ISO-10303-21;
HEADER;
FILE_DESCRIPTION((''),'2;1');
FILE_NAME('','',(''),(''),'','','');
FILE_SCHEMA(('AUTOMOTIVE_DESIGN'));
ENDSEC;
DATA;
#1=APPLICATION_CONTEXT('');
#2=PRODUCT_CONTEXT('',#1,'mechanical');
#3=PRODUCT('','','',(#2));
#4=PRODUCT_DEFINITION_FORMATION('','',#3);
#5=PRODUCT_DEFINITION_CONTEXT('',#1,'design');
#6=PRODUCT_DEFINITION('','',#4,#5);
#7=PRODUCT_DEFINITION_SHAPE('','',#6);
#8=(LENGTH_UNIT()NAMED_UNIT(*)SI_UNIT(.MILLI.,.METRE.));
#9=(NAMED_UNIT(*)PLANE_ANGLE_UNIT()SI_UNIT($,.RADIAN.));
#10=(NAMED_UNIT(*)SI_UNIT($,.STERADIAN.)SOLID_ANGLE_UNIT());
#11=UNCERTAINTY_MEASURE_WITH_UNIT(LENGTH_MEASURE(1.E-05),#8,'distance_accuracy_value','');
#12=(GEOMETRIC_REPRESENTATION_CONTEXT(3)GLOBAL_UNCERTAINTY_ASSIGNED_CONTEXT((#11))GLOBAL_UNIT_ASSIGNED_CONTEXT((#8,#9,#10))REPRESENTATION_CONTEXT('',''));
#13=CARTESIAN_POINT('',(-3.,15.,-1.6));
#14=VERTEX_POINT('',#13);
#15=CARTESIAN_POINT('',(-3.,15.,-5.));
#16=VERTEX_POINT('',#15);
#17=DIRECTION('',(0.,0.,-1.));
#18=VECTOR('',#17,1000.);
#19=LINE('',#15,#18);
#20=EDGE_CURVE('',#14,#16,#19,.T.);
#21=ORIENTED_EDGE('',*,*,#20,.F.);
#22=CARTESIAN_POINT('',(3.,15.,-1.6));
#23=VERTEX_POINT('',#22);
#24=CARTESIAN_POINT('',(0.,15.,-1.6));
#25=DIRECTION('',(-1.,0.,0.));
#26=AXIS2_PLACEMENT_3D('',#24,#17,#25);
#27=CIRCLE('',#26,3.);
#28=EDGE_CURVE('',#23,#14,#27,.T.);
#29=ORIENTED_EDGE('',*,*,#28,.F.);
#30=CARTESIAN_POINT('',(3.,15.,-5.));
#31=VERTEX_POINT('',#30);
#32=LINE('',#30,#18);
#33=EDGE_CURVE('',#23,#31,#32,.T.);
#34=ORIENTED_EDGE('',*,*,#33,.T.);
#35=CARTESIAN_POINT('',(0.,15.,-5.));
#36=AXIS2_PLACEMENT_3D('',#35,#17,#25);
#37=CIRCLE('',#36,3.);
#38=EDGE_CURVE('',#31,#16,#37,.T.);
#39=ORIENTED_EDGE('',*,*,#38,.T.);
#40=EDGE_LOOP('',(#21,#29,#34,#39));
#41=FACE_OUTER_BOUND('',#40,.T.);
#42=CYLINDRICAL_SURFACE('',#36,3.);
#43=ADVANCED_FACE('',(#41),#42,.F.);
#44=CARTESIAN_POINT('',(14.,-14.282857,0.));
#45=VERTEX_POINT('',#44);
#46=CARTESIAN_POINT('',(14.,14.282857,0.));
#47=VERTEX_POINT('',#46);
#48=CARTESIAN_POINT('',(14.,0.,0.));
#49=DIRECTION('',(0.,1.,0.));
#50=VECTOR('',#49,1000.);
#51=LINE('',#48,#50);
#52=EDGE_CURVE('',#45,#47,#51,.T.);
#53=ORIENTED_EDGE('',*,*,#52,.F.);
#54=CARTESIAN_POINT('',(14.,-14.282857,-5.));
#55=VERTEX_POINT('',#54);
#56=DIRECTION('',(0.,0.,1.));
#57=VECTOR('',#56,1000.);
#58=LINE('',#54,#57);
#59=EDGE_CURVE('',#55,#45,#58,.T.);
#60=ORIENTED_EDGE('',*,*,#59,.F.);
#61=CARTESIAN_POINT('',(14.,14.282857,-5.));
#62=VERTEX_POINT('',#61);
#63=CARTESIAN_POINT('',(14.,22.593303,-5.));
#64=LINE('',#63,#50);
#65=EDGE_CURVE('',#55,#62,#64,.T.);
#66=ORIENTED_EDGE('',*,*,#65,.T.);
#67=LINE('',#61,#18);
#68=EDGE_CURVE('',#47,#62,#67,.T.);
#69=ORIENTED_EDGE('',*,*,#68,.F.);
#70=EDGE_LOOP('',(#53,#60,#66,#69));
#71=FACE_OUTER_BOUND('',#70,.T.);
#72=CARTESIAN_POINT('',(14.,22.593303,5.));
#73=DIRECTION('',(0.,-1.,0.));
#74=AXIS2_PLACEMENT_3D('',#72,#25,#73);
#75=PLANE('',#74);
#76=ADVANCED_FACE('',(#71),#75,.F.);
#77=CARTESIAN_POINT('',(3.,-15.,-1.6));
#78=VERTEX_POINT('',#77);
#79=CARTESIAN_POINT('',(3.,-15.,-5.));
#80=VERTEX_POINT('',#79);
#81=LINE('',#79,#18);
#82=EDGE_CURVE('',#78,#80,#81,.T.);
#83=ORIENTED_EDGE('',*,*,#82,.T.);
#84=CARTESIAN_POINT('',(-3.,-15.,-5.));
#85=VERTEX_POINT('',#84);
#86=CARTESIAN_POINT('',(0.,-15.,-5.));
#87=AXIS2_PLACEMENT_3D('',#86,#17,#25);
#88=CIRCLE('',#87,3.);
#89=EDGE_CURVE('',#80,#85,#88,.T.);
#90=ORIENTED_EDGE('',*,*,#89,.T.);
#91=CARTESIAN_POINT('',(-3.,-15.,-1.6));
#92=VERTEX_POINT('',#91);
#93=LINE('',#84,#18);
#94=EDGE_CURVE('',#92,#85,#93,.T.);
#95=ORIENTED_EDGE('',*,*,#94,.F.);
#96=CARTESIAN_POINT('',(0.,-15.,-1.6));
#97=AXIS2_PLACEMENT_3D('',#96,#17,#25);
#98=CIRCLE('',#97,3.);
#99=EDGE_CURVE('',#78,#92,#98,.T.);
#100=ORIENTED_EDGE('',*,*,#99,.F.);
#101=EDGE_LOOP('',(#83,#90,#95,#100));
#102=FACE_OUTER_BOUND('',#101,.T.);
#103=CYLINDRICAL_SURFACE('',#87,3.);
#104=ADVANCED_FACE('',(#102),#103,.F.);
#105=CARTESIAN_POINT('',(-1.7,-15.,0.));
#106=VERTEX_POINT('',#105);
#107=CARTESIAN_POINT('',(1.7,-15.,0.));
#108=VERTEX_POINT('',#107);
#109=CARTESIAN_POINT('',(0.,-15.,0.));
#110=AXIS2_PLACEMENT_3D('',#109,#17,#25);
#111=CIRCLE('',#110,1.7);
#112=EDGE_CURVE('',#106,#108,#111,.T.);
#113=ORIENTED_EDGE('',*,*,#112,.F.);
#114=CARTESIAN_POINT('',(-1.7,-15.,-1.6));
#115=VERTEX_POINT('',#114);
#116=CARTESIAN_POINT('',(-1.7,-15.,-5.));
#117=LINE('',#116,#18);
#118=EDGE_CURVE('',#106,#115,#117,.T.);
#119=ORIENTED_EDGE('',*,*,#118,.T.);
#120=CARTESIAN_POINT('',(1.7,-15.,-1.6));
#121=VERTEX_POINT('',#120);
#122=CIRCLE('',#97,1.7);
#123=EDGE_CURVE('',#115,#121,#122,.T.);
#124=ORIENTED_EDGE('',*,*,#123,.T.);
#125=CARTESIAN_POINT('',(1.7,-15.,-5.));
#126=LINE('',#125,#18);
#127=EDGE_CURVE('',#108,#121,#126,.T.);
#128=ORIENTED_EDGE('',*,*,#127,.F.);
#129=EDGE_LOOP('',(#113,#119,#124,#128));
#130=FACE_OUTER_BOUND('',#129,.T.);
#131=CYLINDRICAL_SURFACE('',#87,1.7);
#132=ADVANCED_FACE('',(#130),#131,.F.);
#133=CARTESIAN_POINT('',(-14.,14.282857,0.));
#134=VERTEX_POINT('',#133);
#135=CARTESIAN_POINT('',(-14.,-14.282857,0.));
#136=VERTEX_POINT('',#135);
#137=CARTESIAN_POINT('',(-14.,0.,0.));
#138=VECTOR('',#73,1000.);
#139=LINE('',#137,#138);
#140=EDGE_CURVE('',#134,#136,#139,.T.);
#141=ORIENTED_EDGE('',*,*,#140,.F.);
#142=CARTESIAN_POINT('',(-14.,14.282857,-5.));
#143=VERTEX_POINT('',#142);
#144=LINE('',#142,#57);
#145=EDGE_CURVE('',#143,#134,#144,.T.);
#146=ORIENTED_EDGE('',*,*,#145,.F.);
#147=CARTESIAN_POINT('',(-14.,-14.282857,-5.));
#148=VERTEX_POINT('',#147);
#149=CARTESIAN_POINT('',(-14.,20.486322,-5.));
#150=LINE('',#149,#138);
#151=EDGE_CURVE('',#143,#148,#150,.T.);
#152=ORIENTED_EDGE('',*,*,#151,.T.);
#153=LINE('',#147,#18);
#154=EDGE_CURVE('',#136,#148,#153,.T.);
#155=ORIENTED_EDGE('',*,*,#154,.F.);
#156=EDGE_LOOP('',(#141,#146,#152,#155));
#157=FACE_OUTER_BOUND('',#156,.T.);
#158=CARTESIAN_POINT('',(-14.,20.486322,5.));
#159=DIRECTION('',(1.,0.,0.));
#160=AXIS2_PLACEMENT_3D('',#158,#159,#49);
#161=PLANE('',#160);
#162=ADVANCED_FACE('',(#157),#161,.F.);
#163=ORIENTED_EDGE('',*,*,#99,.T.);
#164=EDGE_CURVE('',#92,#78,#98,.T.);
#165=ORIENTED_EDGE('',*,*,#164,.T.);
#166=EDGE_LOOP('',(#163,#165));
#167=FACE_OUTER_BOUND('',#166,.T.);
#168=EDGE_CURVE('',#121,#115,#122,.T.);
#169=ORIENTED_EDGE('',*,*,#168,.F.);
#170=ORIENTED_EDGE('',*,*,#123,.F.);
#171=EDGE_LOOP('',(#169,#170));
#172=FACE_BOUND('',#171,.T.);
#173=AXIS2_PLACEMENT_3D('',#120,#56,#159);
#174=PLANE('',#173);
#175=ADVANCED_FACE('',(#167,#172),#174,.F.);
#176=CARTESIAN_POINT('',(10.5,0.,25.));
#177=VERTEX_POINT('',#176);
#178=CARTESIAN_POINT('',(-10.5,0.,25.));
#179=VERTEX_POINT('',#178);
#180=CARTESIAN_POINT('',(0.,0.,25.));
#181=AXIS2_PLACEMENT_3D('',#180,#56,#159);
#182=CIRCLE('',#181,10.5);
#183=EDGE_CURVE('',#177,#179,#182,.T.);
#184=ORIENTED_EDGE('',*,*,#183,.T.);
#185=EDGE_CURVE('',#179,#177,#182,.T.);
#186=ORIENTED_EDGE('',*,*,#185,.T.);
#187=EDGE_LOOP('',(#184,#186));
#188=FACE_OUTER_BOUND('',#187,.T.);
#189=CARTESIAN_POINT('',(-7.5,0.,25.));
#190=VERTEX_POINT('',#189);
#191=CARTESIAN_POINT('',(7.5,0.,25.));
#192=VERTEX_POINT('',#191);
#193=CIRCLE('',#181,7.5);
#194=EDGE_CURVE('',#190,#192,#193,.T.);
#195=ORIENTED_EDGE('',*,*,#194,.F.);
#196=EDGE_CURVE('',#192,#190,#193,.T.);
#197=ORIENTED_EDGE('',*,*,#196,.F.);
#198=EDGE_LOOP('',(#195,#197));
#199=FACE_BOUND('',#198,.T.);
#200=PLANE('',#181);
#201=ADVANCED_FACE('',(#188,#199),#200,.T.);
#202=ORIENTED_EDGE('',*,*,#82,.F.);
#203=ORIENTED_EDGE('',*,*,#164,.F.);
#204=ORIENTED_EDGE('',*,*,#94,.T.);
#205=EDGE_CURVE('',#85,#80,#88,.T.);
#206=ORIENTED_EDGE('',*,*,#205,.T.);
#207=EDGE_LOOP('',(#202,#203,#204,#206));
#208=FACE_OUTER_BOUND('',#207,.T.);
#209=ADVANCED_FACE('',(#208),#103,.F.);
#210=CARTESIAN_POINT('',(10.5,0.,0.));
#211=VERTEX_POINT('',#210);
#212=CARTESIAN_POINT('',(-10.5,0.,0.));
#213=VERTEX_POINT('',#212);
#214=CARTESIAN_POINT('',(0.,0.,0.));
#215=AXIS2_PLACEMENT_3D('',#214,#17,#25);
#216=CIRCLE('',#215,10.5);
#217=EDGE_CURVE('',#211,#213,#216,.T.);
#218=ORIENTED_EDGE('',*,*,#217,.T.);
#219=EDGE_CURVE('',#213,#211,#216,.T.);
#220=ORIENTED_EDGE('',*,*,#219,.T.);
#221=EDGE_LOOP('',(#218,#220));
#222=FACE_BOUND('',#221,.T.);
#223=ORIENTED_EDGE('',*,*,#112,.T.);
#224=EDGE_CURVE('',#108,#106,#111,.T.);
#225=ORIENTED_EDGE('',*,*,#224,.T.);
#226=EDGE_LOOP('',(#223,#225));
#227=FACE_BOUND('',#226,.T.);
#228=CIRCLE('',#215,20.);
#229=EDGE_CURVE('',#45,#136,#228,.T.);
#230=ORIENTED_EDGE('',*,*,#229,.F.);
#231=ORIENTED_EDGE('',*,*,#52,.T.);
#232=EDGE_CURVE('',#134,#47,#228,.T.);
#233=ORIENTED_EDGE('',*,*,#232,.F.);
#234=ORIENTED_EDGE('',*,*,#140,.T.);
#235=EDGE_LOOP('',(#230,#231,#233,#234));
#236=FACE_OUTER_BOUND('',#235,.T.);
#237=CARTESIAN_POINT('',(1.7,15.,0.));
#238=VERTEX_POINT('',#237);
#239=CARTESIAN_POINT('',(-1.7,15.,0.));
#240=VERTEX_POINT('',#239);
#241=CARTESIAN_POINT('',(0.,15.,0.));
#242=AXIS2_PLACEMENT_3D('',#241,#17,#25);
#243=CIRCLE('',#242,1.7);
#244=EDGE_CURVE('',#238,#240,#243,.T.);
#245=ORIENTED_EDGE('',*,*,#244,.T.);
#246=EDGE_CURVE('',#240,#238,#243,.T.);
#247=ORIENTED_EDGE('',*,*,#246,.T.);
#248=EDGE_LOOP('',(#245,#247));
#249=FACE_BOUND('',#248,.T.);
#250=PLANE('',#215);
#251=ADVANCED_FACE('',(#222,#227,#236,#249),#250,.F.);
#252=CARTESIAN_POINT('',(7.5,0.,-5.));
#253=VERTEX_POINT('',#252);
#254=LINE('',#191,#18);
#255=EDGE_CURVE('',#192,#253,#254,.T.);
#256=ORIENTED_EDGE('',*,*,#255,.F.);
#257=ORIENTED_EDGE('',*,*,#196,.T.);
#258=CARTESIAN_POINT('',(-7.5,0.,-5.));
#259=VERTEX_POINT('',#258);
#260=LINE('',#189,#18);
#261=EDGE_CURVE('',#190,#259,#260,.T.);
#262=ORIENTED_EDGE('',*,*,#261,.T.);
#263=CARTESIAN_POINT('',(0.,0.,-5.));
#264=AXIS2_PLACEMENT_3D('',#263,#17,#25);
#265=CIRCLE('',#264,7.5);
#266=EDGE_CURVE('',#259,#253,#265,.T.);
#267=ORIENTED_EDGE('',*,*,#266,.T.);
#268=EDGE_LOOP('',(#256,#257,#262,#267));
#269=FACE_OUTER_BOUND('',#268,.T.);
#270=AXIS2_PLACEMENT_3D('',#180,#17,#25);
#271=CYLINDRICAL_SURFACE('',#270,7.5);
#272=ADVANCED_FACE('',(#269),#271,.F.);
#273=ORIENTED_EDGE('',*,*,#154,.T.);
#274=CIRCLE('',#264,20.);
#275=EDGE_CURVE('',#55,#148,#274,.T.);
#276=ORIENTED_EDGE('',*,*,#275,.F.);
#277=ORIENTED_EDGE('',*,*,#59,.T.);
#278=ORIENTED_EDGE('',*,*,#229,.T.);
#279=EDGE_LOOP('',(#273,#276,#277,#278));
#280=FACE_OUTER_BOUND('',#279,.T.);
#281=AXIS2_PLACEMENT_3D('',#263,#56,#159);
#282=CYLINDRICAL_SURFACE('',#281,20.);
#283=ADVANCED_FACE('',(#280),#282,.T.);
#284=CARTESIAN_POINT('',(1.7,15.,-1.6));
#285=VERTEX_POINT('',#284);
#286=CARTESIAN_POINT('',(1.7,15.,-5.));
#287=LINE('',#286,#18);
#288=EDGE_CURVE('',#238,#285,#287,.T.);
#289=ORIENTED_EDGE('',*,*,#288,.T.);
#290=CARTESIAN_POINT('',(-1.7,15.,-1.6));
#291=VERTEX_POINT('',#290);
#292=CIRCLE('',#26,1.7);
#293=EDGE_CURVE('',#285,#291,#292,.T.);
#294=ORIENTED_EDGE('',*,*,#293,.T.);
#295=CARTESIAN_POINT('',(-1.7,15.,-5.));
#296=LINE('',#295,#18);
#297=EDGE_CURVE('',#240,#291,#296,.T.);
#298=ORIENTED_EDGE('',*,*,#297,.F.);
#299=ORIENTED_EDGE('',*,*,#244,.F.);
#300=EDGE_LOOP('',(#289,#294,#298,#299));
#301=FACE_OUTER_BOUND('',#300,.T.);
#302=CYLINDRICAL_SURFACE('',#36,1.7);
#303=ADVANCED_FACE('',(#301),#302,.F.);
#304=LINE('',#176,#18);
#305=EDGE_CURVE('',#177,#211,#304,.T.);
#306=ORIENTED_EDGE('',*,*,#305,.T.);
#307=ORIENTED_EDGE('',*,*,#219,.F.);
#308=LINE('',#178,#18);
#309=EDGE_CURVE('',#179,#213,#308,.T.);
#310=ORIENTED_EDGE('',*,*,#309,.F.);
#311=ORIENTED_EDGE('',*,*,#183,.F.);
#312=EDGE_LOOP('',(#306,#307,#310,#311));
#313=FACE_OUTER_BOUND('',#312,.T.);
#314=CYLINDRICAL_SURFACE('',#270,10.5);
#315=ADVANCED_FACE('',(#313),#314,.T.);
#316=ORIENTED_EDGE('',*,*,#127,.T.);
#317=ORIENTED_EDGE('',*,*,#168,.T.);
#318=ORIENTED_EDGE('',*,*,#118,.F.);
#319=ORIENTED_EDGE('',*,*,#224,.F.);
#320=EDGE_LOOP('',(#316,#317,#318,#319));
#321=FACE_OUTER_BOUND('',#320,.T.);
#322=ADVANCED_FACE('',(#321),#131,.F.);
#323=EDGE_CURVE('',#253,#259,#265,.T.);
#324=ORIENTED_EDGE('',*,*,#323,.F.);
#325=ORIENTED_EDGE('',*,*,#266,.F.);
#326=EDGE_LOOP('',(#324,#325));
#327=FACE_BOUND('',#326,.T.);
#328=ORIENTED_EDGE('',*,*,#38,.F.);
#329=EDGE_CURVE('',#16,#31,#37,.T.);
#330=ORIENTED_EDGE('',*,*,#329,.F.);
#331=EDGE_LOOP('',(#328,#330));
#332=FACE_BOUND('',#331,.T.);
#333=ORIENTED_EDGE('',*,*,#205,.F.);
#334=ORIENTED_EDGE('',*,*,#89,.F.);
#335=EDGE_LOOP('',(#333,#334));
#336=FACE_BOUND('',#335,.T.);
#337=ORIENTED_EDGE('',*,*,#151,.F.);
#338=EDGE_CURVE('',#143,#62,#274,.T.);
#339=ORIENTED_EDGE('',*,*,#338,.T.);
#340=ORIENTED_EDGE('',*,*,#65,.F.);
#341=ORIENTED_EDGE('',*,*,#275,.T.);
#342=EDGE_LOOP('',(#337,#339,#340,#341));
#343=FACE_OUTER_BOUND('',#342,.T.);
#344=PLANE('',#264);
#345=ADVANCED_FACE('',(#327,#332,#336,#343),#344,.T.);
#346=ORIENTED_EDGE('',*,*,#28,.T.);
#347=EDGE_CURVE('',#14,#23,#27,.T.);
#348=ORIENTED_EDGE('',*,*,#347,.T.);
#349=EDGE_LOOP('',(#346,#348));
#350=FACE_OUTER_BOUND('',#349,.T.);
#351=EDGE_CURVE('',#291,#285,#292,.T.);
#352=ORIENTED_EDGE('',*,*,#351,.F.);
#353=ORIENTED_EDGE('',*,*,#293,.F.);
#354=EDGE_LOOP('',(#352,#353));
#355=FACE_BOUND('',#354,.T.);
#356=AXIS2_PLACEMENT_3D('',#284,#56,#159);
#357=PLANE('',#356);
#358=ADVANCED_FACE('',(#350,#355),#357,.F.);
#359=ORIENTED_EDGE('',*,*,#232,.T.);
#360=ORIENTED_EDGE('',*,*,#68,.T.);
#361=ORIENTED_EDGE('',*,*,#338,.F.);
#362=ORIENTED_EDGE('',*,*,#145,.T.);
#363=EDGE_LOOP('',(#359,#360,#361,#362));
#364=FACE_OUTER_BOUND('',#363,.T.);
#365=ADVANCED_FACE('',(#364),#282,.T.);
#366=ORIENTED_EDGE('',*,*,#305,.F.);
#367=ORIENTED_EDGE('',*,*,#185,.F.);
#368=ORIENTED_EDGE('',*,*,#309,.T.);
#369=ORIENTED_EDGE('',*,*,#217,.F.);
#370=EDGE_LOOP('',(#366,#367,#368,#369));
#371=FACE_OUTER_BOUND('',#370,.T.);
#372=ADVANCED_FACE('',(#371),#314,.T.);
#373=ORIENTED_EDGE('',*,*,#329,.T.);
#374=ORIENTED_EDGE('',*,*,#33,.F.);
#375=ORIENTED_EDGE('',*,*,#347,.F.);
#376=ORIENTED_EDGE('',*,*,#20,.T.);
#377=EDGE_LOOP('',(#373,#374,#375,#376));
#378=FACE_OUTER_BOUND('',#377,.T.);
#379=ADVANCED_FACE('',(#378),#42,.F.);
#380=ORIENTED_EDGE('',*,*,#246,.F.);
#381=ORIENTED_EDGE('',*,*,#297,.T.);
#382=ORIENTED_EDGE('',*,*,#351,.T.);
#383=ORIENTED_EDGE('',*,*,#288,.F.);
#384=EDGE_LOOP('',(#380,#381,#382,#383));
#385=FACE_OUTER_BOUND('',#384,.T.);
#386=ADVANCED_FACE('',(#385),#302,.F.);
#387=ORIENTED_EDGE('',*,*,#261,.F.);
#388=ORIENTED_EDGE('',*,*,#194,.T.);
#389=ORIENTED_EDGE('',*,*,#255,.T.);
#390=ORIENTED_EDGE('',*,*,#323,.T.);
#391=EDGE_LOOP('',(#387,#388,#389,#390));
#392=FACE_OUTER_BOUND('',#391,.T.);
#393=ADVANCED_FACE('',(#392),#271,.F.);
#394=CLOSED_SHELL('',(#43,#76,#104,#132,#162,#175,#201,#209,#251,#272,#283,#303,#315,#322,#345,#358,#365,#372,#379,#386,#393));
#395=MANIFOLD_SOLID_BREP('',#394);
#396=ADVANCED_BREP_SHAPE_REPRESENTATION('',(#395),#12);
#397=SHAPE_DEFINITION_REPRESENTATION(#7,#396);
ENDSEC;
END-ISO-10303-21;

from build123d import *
from build123d.topology import SkipClean

# Parameters (mm, degrees)
SKETCH_1_R                = 10.5
SKETCH_1_R_2              = 7.5
EXTRUDE_1_DEPTH           = 25
EXTRUDE_START             = 5
SKETCH_3_R                = 20
SKETCH_3_R_2              = 7.5
EXTRUDE_3_DEPTH           = 5
HOLE_WIZARD_1_D           = 3.4
HOLE_WIZARD_1_CBORE_D     = 6
HOLE_WIZARD_1_CBORE_DEPTH = 3.4
SKETCH_6_W                = 10.726446136
SKETCH_6_H                = 40.511488533
SKETCH_6_W_2              = 7.853290921
SKETCH_6_H_2              = 42.714240865
CUT_EXTRUDE_1_DEPTH       = 10


with BuildPart() as part:
    # 草图1 → 凸台-拉伸1 (new body)
    with BuildSketch(Plane.XY):
        Circle(SKETCH_1_R)
        Circle(SKETCH_1_R_2, mode=Mode.SUBTRACT)
    extrude(amount=EXTRUDE_1_DEPTH)

    # 草图3 → 凸台-拉伸3 (add)
    with SkipClean():  # the faces are left unmerged after this step: merging them gives an invalid solid
        with BuildSketch(Plane(origin=(0, 0, 0), x_dir=(-1, 0, 0), z_dir=(0, 0, -1)).offset(EXTRUDE_START)):
            Circle(SKETCH_3_R)
            Circle(SKETCH_3_R_2, mode=Mode.SUBTRACT)
        extrude(amount=-EXTRUDE_3_DEPTH)

    # 打孔尺寸根据内六角圆柱头螺钉的类型1 (through all)
    with Locations(Plane(origin=(0, 0, -5), x_dir=(-1, 0, 0), z_dir=(0, 0, -1))):
        with Locations((0, 15), (0, -15)):
            CounterBoreHole(HOLE_WIZARD_1_D / 2, HOLE_WIZARD_1_CBORE_D / 2, HOLE_WIZARD_1_CBORE_DEPTH)

    # 草图6 → 切除-拉伸1 (cut)
    with SkipClean():  # the faces are left unmerged after this step: merging them gives an invalid solid
        with BuildSketch(Plane(origin=(0, 0, -5), x_dir=(-1, 0, 0), z_dir=(0, 0, -1))):
            with Locations((-19.363223068, 2.337558383)):
                Rectangle(SKETCH_6_W, SKETCH_6_H)
            with Locations((17.926645461, -0.870798275)):
                Rectangle(SKETCH_6_W_2, SKETCH_6_H_2)
        extrude(amount=-CUT_EXTRUDE_1_DEPTH, mode=Mode.SUBTRACT)


solid = part.part
